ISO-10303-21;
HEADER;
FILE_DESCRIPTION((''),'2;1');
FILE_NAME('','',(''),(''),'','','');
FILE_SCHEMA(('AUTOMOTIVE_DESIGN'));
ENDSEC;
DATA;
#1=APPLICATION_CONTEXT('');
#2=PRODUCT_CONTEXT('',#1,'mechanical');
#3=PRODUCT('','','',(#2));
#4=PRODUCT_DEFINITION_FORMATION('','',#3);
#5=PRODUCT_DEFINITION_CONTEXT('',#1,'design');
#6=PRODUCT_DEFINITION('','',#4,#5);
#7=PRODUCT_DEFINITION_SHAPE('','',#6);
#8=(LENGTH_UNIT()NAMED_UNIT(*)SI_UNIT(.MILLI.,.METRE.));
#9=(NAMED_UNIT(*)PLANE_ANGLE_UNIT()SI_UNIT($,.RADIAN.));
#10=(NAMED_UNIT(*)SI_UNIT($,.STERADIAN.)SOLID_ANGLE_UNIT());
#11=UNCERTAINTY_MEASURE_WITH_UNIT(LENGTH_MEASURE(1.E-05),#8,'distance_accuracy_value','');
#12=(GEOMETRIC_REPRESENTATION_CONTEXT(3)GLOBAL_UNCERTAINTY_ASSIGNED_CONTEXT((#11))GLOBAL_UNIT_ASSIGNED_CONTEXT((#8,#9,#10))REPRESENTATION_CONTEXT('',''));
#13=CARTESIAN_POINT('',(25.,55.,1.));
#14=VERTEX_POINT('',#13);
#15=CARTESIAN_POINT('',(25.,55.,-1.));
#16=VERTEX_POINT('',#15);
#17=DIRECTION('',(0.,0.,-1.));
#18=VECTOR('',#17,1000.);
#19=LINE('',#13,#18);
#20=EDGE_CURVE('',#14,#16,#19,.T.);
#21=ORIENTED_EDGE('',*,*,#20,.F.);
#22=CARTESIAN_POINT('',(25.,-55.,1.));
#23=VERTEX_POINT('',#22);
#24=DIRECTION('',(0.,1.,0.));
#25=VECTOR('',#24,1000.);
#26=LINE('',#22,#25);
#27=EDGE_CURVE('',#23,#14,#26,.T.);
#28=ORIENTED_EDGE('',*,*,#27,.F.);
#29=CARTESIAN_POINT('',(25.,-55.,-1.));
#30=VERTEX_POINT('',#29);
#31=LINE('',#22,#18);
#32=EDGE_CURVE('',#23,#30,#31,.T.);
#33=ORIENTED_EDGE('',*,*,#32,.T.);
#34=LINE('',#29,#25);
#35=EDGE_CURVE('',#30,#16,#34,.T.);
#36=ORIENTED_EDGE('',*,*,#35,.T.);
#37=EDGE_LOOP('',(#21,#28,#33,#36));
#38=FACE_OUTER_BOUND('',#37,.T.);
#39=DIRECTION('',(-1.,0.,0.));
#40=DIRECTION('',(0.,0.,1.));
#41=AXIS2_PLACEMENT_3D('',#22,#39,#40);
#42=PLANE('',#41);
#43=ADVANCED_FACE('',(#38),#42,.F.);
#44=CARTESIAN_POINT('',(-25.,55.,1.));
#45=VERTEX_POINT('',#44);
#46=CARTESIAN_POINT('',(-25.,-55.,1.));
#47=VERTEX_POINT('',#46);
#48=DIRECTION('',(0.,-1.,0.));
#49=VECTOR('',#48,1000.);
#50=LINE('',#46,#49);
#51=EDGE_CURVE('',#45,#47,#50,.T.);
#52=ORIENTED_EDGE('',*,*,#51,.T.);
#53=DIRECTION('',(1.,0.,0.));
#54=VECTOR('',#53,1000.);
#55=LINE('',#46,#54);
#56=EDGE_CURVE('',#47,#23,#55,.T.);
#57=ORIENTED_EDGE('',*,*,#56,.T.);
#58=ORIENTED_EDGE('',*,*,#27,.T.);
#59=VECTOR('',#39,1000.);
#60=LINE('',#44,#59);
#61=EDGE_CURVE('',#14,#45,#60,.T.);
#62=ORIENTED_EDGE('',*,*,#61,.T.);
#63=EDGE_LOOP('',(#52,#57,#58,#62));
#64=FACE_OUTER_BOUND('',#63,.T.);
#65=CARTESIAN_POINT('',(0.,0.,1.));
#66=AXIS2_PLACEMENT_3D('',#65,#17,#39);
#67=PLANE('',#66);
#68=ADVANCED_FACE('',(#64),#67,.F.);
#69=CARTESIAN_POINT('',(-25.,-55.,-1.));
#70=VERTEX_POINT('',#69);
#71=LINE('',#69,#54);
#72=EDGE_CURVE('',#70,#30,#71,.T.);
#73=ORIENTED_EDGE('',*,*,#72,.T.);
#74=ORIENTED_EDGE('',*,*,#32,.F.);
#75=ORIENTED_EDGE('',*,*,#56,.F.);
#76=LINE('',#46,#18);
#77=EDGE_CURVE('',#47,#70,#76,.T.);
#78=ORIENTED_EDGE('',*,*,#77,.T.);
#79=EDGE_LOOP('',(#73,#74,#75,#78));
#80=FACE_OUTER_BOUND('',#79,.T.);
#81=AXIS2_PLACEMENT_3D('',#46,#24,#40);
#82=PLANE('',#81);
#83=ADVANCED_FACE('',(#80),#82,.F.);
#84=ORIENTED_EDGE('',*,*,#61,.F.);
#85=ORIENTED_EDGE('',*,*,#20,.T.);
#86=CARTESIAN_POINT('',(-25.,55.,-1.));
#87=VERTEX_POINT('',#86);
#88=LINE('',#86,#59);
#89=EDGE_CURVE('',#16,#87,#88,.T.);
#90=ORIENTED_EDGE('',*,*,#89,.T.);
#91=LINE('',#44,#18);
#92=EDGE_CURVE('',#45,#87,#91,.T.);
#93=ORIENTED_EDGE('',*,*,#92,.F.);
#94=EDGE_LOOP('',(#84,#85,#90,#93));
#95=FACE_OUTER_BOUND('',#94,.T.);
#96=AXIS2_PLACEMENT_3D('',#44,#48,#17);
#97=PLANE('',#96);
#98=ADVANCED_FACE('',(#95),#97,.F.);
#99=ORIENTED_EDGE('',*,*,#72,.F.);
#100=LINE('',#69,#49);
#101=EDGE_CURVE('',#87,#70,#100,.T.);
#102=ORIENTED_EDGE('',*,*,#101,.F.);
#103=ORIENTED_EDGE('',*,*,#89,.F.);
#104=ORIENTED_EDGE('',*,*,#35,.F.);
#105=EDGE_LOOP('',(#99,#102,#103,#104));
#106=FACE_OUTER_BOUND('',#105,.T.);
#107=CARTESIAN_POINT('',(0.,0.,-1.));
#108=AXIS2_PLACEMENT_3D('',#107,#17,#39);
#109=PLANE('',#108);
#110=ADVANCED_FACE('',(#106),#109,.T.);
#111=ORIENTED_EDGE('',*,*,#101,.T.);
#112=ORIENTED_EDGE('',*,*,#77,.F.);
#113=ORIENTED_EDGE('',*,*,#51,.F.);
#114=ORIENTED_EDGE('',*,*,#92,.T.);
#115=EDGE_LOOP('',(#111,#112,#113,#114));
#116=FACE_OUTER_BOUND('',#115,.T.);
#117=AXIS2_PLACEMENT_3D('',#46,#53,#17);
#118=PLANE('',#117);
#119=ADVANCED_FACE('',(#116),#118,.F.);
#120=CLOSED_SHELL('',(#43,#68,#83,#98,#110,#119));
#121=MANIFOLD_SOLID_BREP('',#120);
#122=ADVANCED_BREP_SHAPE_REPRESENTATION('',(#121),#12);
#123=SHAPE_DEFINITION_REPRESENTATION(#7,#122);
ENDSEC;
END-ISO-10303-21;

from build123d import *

# Parameters (mm, degrees)
SKETCH_1_W      = 50
SKETCH_1_H      = 110
EXTRUDE_1_DEPTH = 1


with BuildPart() as part:
    # 草图1 → 凸台-拉伸1 (new, symmetric)
    with BuildSketch(Plane.XY):
        Rectangle(SKETCH_1_W, SKETCH_1_H)
    extrude(amount=EXTRUDE_1_DEPTH, both=True)


solid = part.part
